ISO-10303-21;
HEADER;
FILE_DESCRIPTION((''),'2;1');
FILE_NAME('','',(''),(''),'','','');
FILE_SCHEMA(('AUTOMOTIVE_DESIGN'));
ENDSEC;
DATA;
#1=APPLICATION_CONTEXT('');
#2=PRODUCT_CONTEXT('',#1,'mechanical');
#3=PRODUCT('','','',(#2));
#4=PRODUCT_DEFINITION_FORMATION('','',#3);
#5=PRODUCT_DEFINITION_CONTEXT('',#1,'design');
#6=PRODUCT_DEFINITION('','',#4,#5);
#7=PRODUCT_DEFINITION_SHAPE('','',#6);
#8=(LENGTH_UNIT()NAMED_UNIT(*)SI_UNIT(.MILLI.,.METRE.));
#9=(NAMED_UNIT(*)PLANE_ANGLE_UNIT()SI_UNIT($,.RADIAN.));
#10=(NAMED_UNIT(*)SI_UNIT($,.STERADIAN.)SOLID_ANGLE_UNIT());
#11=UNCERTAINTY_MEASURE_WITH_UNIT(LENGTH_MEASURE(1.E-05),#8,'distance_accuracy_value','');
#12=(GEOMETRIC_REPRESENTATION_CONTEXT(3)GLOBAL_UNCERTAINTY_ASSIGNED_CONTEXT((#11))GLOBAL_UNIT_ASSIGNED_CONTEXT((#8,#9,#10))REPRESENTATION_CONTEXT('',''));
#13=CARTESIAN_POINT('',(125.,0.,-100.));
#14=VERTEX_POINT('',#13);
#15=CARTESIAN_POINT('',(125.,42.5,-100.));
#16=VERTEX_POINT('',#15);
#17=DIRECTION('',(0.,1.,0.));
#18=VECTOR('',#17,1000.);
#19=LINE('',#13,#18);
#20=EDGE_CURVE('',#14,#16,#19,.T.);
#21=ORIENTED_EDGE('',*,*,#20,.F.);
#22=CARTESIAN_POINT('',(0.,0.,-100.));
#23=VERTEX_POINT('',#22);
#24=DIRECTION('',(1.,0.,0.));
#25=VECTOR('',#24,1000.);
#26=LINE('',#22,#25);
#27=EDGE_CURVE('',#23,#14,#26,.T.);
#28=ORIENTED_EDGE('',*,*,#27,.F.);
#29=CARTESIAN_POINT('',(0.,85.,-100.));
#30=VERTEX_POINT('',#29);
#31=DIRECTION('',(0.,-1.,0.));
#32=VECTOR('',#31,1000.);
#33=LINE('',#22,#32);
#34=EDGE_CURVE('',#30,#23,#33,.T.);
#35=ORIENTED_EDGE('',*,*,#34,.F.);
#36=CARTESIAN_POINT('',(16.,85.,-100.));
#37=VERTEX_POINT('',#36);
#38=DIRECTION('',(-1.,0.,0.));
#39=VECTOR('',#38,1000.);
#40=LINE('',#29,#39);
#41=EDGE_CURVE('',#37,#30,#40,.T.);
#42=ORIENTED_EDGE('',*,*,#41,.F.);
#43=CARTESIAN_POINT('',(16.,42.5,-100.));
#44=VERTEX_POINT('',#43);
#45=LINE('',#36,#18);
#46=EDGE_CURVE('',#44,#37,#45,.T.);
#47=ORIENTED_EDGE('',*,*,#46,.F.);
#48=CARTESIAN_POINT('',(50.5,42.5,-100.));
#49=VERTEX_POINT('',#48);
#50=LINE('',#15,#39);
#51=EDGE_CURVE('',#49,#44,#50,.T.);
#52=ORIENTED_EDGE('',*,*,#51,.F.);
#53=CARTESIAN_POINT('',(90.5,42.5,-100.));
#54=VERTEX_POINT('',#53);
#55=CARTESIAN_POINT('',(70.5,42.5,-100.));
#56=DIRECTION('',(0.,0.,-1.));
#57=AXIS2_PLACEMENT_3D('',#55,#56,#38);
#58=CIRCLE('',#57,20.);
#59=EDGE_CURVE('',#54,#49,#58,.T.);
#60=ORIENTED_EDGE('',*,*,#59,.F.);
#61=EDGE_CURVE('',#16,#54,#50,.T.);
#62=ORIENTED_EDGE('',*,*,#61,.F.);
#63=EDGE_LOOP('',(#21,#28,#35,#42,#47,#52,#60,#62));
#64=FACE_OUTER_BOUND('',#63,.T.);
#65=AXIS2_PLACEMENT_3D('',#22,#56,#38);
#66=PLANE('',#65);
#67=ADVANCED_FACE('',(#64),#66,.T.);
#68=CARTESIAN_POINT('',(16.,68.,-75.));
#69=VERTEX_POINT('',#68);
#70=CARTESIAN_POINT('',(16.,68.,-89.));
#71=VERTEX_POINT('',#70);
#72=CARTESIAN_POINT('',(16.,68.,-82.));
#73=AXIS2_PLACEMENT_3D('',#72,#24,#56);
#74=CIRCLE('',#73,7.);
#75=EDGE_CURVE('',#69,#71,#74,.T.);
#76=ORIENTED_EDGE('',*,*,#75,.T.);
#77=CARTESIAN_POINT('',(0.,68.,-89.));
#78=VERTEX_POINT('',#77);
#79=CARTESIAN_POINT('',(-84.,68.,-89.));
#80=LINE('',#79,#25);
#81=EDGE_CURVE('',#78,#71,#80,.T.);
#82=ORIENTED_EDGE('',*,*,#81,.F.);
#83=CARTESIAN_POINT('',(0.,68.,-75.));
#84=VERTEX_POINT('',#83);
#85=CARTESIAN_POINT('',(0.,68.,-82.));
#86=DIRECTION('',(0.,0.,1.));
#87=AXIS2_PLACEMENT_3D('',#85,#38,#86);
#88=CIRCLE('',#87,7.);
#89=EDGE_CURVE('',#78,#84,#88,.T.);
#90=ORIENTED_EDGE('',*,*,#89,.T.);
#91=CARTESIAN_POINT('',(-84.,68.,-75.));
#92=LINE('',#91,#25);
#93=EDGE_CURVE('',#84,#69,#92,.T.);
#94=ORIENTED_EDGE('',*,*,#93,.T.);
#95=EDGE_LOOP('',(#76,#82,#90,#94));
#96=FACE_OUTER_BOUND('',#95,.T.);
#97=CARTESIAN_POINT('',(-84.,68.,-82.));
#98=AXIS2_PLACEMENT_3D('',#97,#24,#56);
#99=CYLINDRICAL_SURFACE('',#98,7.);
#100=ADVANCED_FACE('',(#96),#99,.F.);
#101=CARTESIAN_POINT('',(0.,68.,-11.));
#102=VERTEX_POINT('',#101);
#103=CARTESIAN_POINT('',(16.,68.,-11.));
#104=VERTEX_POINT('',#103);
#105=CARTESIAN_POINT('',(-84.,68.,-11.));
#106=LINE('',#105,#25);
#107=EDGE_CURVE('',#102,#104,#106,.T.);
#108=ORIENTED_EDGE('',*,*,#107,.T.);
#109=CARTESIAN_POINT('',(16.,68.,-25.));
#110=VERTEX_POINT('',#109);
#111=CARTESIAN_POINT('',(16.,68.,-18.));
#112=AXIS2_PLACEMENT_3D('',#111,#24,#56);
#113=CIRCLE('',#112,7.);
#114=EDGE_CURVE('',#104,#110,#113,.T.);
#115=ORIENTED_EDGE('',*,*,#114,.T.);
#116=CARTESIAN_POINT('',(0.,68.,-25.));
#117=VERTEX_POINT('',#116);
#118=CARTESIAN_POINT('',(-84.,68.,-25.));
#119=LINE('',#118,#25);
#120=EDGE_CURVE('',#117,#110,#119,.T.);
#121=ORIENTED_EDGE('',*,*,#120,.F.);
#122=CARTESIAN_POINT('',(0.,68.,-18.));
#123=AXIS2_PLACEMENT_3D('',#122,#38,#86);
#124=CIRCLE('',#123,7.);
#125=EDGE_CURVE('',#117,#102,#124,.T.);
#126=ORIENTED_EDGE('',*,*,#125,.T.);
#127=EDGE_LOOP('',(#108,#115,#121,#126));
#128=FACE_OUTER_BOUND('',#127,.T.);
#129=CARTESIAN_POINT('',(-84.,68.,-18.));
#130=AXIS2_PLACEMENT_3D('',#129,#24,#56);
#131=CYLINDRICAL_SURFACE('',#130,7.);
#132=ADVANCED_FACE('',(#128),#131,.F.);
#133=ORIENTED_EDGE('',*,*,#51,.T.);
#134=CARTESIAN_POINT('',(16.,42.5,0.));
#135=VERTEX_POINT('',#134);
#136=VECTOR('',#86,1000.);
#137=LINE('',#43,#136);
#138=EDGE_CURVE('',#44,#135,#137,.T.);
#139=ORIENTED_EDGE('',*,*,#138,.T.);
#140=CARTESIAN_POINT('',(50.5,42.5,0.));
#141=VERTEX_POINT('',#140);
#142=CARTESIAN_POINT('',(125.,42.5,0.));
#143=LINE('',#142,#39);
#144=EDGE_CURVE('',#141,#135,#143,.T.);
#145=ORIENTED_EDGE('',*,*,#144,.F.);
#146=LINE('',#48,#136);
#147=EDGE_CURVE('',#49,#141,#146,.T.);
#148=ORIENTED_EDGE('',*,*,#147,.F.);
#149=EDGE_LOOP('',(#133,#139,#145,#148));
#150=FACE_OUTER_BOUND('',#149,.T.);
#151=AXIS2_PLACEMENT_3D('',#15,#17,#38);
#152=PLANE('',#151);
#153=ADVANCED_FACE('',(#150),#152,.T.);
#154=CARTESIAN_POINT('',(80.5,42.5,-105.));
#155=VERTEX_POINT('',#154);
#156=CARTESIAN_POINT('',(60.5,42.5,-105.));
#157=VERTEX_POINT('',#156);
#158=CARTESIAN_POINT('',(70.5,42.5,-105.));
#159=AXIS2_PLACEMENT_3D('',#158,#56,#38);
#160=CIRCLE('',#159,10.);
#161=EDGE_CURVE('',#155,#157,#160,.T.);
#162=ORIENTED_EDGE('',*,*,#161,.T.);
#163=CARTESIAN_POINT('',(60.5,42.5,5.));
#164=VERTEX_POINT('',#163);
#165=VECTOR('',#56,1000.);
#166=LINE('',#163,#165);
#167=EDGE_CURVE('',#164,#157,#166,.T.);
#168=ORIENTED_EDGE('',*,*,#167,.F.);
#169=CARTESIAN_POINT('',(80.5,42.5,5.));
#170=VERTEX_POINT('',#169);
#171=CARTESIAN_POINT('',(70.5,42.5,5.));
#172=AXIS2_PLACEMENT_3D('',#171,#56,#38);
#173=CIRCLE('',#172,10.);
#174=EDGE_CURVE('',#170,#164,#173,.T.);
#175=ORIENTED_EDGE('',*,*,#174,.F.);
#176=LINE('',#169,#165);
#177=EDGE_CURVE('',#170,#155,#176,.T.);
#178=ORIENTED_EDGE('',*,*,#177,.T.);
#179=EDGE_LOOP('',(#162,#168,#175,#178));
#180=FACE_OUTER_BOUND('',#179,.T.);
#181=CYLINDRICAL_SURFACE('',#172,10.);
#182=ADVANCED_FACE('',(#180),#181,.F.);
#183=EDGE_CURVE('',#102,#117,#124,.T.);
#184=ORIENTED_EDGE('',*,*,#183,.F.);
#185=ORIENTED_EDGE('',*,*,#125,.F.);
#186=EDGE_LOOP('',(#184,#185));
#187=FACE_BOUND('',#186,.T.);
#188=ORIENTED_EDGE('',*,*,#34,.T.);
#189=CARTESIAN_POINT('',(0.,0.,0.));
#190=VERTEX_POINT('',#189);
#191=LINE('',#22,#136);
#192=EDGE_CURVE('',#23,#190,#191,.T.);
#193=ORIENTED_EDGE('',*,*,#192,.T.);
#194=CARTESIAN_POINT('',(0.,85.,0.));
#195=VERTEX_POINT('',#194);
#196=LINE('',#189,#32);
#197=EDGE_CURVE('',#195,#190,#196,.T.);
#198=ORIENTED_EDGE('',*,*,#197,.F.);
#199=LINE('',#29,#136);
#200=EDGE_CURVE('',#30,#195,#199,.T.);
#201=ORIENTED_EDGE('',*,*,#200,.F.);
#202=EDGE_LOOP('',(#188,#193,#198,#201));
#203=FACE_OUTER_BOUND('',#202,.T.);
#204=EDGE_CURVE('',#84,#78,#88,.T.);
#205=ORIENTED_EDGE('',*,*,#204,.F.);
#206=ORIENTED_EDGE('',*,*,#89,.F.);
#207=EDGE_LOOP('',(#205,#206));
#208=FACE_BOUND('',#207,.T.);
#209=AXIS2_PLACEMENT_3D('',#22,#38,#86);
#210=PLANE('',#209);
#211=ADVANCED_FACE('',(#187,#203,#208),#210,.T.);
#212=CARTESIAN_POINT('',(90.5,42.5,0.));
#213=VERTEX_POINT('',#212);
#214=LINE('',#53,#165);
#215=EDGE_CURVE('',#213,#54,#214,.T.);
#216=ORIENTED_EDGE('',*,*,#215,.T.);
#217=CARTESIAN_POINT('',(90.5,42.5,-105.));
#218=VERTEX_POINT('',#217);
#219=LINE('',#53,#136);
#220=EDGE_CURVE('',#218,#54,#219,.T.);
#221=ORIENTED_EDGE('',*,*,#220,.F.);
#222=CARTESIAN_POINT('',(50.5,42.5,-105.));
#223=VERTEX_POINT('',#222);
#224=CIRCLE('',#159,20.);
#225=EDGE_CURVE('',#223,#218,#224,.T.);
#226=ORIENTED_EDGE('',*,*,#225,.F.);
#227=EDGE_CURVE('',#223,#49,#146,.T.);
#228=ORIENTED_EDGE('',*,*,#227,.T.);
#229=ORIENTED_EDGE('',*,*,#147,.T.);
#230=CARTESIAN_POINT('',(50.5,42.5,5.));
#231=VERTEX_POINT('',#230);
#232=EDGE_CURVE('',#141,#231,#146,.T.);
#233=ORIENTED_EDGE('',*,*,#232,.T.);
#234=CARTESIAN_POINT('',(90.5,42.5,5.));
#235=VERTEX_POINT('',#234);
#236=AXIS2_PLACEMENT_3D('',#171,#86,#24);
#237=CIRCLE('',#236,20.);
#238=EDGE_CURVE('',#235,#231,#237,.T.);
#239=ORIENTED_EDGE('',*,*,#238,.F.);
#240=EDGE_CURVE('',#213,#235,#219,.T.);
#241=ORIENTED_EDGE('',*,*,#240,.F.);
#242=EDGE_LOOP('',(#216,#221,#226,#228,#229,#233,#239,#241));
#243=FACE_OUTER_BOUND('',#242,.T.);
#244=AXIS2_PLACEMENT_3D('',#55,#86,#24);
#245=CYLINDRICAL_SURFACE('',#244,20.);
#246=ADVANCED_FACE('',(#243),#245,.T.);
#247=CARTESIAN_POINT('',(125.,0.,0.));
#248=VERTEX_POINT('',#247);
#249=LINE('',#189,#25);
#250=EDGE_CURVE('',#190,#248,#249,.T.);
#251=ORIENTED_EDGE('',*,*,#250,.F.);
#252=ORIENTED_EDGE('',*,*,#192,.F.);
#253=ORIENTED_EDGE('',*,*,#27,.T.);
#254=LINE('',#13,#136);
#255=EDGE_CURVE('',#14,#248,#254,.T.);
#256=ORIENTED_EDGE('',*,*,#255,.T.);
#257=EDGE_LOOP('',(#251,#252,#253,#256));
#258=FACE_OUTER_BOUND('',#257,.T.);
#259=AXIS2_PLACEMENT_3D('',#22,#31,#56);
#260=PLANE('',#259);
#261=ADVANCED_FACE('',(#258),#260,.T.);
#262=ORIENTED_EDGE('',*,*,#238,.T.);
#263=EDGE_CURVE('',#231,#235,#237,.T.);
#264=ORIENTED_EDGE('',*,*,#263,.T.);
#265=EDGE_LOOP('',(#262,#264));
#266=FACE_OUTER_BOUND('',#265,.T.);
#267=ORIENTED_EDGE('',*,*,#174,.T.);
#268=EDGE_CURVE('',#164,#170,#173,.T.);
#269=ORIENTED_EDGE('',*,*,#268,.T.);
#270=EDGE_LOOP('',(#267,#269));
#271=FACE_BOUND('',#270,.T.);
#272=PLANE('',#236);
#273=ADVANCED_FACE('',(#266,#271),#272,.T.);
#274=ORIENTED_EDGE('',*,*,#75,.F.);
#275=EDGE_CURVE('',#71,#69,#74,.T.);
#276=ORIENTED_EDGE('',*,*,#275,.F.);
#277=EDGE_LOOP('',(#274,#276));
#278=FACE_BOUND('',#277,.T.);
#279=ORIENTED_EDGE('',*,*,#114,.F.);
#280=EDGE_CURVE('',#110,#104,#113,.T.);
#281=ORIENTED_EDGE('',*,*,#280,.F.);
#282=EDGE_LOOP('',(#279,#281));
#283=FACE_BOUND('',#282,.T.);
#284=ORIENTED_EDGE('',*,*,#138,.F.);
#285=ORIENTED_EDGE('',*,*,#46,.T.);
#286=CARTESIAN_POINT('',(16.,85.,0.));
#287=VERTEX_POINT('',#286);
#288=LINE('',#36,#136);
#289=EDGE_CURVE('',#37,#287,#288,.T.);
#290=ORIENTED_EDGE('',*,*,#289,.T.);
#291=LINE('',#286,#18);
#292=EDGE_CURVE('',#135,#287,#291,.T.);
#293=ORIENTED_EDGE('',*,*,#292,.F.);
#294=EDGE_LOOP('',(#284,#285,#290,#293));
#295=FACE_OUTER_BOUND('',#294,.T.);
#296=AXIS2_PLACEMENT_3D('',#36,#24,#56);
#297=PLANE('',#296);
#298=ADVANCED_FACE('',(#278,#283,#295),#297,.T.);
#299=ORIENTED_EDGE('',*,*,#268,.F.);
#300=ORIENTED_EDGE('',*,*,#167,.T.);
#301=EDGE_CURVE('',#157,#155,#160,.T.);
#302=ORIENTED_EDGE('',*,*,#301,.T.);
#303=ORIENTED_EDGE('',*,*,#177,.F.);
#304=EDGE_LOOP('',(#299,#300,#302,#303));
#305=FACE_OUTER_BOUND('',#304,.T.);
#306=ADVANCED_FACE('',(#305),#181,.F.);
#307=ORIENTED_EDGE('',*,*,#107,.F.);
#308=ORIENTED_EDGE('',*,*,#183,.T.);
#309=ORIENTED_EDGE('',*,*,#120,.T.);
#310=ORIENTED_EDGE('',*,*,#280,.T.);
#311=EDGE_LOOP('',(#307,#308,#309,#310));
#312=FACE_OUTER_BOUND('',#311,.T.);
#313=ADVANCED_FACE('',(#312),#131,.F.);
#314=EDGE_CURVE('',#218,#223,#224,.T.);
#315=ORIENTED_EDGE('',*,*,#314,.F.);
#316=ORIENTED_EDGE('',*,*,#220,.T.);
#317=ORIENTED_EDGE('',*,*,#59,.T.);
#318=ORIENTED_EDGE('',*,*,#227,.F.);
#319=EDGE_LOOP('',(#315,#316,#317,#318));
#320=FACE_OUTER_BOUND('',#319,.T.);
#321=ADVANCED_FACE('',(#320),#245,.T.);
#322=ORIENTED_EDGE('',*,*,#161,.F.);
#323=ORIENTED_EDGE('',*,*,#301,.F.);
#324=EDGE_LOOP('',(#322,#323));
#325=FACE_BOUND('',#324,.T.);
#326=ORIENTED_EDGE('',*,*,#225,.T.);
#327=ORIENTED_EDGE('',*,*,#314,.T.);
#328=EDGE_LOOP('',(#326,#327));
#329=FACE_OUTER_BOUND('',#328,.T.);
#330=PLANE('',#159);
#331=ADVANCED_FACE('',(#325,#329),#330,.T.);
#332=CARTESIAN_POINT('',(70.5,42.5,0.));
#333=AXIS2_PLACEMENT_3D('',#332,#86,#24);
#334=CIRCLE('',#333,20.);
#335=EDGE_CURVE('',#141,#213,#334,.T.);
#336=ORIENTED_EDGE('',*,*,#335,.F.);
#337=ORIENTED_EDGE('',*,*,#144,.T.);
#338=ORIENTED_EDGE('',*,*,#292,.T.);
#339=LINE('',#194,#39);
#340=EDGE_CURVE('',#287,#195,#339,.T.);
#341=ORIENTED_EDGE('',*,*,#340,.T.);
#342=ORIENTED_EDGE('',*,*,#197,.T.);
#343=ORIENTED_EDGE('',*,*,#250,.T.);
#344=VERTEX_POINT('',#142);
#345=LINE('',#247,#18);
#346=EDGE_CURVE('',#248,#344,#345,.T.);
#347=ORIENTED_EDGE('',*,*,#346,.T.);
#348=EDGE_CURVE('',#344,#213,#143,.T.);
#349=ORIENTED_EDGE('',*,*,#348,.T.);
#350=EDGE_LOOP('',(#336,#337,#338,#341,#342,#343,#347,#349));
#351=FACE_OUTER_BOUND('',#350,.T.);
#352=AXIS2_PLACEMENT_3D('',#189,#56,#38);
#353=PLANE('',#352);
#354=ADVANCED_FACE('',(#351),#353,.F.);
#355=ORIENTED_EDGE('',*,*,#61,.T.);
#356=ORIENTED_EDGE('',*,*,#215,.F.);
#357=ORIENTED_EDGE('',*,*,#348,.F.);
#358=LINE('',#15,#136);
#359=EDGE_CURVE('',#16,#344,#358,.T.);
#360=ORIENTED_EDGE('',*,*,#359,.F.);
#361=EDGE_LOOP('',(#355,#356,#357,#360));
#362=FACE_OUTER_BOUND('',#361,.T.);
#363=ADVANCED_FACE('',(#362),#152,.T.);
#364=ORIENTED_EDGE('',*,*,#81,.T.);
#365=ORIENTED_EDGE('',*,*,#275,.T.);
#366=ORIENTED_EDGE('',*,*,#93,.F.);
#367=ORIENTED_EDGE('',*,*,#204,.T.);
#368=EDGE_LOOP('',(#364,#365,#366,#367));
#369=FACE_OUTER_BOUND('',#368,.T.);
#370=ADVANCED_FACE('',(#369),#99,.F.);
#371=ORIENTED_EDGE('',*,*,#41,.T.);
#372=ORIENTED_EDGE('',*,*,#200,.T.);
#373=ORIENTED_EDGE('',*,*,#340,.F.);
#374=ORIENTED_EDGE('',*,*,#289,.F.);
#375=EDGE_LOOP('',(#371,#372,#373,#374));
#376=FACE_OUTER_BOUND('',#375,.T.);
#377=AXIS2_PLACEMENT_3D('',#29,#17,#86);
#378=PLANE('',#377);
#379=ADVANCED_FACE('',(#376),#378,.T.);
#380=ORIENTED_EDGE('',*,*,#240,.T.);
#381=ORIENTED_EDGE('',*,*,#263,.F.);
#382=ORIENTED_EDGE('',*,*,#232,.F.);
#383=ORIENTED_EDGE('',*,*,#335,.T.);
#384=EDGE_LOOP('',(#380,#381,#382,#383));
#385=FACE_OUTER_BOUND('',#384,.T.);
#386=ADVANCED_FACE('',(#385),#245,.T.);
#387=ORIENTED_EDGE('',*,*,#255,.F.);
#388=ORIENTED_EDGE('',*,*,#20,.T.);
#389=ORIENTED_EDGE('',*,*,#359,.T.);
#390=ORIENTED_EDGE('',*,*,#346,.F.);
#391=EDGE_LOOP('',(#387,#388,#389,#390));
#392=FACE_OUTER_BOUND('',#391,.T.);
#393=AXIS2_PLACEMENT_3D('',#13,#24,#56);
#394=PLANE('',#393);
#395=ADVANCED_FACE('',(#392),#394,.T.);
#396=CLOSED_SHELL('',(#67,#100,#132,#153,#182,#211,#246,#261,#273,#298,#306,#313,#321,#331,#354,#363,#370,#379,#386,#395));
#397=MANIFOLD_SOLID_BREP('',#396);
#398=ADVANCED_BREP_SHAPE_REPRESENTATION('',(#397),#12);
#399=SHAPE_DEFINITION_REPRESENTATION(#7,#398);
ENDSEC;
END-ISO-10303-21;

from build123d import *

# Parameters (mm, degrees)
L_BRACKET_BODY_DEPTH           = 100
MOUNTING_HOLES_SKETCH_R        = 7
MOUNTING_HOLES_2X_14_DEPTH     = 100
TRUNNION_SKETCH_R              = 20
TRUNNION_40_DEPTH              = 100
TRUNNION_START                 = 5
TRUNNION_END_BOSS_A_SKETCH_R   = 20
TRUNNION_END_BOSS_A_40X5_DEPTH = 5
TRUNNION_END_BOSS_B_SKETCH_R   = 20
TRUNNION_END_BOSS_B_40X5_DEPTH = 5
TRUNNION_BORE_SKETCH_R         = 10
TRUNNION_BORE_20_DEPTH         = 110


with BuildPart() as part:
    # L Bracket Profile Sketch → L Bracket Body (new body)
    with BuildSketch(Plane.XY):
        Polygon((0, 0), (125, 0), (125, 42.5), (16, 42.5), (16, 85), (0, 85), align=None)
    extrude(amount=-L_BRACKET_BODY_DEPTH)

    # Mounting Holes Sketch → Mounting Holes 2xØ14 (cut)
    with BuildSketch(Plane(origin=(16, 0, 0), x_dir=(0, 0, -1), z_dir=(1, 0, 0))):
        with Locations((18, 68)):
            Circle(MOUNTING_HOLES_SKETCH_R)
        with Locations((82, 68)):
            Circle(MOUNTING_HOLES_SKETCH_R)
    extrude(amount=-MOUNTING_HOLES_2X_14_DEPTH, mode=Mode.SUBTRACT)

    # Trunnion Sketch → Trunnion Ø40 (add)
    with BuildSketch(Plane.XY):
        with Locations((70.5, 42.5)):
            Circle(TRUNNION_SKETCH_R)
    extrude(amount=-TRUNNION_40_DEPTH)

    # Trunnion End Boss A Sketch → Trunnion End Boss A Ø40x5 (add)
    with BuildSketch(Plane.XY.offset(TRUNNION_START)):
        with Locations((70.5, 42.5)):
            Circle(TRUNNION_END_BOSS_A_SKETCH_R)
    extrude(amount=-TRUNNION_END_BOSS_A_40X5_DEPTH)

    # Trunnion End Boss B Sketch → Trunnion End Boss B Ø40x5 (add)
    with BuildSketch(Plane(origin=(0, 0, -100), x_dir=(-1, 0, 0), z_dir=(0, 0, -1))):
        with Locations(Location((-70.5, 42.5, 0), (0, 0, 180))):
            Circle(TRUNNION_END_BOSS_B_SKETCH_R)
    extrude(amount=TRUNNION_END_BOSS_B_40X5_DEPTH)

    # Trunnion Bore Sketch → Trunnion Bore Ø20 (cut)
    with BuildSketch(Plane(origin=(0, 0, -105), x_dir=(-1, 0, 0), z_dir=(0, 0, -1))):
        with Locations((-70.5, 42.5)):
            Circle(TRUNNION_BORE_SKETCH_R)
    extrude(amount=-TRUNNION_BORE_20_DEPTH, mode=Mode.SUBTRACT)


solid = part.part
